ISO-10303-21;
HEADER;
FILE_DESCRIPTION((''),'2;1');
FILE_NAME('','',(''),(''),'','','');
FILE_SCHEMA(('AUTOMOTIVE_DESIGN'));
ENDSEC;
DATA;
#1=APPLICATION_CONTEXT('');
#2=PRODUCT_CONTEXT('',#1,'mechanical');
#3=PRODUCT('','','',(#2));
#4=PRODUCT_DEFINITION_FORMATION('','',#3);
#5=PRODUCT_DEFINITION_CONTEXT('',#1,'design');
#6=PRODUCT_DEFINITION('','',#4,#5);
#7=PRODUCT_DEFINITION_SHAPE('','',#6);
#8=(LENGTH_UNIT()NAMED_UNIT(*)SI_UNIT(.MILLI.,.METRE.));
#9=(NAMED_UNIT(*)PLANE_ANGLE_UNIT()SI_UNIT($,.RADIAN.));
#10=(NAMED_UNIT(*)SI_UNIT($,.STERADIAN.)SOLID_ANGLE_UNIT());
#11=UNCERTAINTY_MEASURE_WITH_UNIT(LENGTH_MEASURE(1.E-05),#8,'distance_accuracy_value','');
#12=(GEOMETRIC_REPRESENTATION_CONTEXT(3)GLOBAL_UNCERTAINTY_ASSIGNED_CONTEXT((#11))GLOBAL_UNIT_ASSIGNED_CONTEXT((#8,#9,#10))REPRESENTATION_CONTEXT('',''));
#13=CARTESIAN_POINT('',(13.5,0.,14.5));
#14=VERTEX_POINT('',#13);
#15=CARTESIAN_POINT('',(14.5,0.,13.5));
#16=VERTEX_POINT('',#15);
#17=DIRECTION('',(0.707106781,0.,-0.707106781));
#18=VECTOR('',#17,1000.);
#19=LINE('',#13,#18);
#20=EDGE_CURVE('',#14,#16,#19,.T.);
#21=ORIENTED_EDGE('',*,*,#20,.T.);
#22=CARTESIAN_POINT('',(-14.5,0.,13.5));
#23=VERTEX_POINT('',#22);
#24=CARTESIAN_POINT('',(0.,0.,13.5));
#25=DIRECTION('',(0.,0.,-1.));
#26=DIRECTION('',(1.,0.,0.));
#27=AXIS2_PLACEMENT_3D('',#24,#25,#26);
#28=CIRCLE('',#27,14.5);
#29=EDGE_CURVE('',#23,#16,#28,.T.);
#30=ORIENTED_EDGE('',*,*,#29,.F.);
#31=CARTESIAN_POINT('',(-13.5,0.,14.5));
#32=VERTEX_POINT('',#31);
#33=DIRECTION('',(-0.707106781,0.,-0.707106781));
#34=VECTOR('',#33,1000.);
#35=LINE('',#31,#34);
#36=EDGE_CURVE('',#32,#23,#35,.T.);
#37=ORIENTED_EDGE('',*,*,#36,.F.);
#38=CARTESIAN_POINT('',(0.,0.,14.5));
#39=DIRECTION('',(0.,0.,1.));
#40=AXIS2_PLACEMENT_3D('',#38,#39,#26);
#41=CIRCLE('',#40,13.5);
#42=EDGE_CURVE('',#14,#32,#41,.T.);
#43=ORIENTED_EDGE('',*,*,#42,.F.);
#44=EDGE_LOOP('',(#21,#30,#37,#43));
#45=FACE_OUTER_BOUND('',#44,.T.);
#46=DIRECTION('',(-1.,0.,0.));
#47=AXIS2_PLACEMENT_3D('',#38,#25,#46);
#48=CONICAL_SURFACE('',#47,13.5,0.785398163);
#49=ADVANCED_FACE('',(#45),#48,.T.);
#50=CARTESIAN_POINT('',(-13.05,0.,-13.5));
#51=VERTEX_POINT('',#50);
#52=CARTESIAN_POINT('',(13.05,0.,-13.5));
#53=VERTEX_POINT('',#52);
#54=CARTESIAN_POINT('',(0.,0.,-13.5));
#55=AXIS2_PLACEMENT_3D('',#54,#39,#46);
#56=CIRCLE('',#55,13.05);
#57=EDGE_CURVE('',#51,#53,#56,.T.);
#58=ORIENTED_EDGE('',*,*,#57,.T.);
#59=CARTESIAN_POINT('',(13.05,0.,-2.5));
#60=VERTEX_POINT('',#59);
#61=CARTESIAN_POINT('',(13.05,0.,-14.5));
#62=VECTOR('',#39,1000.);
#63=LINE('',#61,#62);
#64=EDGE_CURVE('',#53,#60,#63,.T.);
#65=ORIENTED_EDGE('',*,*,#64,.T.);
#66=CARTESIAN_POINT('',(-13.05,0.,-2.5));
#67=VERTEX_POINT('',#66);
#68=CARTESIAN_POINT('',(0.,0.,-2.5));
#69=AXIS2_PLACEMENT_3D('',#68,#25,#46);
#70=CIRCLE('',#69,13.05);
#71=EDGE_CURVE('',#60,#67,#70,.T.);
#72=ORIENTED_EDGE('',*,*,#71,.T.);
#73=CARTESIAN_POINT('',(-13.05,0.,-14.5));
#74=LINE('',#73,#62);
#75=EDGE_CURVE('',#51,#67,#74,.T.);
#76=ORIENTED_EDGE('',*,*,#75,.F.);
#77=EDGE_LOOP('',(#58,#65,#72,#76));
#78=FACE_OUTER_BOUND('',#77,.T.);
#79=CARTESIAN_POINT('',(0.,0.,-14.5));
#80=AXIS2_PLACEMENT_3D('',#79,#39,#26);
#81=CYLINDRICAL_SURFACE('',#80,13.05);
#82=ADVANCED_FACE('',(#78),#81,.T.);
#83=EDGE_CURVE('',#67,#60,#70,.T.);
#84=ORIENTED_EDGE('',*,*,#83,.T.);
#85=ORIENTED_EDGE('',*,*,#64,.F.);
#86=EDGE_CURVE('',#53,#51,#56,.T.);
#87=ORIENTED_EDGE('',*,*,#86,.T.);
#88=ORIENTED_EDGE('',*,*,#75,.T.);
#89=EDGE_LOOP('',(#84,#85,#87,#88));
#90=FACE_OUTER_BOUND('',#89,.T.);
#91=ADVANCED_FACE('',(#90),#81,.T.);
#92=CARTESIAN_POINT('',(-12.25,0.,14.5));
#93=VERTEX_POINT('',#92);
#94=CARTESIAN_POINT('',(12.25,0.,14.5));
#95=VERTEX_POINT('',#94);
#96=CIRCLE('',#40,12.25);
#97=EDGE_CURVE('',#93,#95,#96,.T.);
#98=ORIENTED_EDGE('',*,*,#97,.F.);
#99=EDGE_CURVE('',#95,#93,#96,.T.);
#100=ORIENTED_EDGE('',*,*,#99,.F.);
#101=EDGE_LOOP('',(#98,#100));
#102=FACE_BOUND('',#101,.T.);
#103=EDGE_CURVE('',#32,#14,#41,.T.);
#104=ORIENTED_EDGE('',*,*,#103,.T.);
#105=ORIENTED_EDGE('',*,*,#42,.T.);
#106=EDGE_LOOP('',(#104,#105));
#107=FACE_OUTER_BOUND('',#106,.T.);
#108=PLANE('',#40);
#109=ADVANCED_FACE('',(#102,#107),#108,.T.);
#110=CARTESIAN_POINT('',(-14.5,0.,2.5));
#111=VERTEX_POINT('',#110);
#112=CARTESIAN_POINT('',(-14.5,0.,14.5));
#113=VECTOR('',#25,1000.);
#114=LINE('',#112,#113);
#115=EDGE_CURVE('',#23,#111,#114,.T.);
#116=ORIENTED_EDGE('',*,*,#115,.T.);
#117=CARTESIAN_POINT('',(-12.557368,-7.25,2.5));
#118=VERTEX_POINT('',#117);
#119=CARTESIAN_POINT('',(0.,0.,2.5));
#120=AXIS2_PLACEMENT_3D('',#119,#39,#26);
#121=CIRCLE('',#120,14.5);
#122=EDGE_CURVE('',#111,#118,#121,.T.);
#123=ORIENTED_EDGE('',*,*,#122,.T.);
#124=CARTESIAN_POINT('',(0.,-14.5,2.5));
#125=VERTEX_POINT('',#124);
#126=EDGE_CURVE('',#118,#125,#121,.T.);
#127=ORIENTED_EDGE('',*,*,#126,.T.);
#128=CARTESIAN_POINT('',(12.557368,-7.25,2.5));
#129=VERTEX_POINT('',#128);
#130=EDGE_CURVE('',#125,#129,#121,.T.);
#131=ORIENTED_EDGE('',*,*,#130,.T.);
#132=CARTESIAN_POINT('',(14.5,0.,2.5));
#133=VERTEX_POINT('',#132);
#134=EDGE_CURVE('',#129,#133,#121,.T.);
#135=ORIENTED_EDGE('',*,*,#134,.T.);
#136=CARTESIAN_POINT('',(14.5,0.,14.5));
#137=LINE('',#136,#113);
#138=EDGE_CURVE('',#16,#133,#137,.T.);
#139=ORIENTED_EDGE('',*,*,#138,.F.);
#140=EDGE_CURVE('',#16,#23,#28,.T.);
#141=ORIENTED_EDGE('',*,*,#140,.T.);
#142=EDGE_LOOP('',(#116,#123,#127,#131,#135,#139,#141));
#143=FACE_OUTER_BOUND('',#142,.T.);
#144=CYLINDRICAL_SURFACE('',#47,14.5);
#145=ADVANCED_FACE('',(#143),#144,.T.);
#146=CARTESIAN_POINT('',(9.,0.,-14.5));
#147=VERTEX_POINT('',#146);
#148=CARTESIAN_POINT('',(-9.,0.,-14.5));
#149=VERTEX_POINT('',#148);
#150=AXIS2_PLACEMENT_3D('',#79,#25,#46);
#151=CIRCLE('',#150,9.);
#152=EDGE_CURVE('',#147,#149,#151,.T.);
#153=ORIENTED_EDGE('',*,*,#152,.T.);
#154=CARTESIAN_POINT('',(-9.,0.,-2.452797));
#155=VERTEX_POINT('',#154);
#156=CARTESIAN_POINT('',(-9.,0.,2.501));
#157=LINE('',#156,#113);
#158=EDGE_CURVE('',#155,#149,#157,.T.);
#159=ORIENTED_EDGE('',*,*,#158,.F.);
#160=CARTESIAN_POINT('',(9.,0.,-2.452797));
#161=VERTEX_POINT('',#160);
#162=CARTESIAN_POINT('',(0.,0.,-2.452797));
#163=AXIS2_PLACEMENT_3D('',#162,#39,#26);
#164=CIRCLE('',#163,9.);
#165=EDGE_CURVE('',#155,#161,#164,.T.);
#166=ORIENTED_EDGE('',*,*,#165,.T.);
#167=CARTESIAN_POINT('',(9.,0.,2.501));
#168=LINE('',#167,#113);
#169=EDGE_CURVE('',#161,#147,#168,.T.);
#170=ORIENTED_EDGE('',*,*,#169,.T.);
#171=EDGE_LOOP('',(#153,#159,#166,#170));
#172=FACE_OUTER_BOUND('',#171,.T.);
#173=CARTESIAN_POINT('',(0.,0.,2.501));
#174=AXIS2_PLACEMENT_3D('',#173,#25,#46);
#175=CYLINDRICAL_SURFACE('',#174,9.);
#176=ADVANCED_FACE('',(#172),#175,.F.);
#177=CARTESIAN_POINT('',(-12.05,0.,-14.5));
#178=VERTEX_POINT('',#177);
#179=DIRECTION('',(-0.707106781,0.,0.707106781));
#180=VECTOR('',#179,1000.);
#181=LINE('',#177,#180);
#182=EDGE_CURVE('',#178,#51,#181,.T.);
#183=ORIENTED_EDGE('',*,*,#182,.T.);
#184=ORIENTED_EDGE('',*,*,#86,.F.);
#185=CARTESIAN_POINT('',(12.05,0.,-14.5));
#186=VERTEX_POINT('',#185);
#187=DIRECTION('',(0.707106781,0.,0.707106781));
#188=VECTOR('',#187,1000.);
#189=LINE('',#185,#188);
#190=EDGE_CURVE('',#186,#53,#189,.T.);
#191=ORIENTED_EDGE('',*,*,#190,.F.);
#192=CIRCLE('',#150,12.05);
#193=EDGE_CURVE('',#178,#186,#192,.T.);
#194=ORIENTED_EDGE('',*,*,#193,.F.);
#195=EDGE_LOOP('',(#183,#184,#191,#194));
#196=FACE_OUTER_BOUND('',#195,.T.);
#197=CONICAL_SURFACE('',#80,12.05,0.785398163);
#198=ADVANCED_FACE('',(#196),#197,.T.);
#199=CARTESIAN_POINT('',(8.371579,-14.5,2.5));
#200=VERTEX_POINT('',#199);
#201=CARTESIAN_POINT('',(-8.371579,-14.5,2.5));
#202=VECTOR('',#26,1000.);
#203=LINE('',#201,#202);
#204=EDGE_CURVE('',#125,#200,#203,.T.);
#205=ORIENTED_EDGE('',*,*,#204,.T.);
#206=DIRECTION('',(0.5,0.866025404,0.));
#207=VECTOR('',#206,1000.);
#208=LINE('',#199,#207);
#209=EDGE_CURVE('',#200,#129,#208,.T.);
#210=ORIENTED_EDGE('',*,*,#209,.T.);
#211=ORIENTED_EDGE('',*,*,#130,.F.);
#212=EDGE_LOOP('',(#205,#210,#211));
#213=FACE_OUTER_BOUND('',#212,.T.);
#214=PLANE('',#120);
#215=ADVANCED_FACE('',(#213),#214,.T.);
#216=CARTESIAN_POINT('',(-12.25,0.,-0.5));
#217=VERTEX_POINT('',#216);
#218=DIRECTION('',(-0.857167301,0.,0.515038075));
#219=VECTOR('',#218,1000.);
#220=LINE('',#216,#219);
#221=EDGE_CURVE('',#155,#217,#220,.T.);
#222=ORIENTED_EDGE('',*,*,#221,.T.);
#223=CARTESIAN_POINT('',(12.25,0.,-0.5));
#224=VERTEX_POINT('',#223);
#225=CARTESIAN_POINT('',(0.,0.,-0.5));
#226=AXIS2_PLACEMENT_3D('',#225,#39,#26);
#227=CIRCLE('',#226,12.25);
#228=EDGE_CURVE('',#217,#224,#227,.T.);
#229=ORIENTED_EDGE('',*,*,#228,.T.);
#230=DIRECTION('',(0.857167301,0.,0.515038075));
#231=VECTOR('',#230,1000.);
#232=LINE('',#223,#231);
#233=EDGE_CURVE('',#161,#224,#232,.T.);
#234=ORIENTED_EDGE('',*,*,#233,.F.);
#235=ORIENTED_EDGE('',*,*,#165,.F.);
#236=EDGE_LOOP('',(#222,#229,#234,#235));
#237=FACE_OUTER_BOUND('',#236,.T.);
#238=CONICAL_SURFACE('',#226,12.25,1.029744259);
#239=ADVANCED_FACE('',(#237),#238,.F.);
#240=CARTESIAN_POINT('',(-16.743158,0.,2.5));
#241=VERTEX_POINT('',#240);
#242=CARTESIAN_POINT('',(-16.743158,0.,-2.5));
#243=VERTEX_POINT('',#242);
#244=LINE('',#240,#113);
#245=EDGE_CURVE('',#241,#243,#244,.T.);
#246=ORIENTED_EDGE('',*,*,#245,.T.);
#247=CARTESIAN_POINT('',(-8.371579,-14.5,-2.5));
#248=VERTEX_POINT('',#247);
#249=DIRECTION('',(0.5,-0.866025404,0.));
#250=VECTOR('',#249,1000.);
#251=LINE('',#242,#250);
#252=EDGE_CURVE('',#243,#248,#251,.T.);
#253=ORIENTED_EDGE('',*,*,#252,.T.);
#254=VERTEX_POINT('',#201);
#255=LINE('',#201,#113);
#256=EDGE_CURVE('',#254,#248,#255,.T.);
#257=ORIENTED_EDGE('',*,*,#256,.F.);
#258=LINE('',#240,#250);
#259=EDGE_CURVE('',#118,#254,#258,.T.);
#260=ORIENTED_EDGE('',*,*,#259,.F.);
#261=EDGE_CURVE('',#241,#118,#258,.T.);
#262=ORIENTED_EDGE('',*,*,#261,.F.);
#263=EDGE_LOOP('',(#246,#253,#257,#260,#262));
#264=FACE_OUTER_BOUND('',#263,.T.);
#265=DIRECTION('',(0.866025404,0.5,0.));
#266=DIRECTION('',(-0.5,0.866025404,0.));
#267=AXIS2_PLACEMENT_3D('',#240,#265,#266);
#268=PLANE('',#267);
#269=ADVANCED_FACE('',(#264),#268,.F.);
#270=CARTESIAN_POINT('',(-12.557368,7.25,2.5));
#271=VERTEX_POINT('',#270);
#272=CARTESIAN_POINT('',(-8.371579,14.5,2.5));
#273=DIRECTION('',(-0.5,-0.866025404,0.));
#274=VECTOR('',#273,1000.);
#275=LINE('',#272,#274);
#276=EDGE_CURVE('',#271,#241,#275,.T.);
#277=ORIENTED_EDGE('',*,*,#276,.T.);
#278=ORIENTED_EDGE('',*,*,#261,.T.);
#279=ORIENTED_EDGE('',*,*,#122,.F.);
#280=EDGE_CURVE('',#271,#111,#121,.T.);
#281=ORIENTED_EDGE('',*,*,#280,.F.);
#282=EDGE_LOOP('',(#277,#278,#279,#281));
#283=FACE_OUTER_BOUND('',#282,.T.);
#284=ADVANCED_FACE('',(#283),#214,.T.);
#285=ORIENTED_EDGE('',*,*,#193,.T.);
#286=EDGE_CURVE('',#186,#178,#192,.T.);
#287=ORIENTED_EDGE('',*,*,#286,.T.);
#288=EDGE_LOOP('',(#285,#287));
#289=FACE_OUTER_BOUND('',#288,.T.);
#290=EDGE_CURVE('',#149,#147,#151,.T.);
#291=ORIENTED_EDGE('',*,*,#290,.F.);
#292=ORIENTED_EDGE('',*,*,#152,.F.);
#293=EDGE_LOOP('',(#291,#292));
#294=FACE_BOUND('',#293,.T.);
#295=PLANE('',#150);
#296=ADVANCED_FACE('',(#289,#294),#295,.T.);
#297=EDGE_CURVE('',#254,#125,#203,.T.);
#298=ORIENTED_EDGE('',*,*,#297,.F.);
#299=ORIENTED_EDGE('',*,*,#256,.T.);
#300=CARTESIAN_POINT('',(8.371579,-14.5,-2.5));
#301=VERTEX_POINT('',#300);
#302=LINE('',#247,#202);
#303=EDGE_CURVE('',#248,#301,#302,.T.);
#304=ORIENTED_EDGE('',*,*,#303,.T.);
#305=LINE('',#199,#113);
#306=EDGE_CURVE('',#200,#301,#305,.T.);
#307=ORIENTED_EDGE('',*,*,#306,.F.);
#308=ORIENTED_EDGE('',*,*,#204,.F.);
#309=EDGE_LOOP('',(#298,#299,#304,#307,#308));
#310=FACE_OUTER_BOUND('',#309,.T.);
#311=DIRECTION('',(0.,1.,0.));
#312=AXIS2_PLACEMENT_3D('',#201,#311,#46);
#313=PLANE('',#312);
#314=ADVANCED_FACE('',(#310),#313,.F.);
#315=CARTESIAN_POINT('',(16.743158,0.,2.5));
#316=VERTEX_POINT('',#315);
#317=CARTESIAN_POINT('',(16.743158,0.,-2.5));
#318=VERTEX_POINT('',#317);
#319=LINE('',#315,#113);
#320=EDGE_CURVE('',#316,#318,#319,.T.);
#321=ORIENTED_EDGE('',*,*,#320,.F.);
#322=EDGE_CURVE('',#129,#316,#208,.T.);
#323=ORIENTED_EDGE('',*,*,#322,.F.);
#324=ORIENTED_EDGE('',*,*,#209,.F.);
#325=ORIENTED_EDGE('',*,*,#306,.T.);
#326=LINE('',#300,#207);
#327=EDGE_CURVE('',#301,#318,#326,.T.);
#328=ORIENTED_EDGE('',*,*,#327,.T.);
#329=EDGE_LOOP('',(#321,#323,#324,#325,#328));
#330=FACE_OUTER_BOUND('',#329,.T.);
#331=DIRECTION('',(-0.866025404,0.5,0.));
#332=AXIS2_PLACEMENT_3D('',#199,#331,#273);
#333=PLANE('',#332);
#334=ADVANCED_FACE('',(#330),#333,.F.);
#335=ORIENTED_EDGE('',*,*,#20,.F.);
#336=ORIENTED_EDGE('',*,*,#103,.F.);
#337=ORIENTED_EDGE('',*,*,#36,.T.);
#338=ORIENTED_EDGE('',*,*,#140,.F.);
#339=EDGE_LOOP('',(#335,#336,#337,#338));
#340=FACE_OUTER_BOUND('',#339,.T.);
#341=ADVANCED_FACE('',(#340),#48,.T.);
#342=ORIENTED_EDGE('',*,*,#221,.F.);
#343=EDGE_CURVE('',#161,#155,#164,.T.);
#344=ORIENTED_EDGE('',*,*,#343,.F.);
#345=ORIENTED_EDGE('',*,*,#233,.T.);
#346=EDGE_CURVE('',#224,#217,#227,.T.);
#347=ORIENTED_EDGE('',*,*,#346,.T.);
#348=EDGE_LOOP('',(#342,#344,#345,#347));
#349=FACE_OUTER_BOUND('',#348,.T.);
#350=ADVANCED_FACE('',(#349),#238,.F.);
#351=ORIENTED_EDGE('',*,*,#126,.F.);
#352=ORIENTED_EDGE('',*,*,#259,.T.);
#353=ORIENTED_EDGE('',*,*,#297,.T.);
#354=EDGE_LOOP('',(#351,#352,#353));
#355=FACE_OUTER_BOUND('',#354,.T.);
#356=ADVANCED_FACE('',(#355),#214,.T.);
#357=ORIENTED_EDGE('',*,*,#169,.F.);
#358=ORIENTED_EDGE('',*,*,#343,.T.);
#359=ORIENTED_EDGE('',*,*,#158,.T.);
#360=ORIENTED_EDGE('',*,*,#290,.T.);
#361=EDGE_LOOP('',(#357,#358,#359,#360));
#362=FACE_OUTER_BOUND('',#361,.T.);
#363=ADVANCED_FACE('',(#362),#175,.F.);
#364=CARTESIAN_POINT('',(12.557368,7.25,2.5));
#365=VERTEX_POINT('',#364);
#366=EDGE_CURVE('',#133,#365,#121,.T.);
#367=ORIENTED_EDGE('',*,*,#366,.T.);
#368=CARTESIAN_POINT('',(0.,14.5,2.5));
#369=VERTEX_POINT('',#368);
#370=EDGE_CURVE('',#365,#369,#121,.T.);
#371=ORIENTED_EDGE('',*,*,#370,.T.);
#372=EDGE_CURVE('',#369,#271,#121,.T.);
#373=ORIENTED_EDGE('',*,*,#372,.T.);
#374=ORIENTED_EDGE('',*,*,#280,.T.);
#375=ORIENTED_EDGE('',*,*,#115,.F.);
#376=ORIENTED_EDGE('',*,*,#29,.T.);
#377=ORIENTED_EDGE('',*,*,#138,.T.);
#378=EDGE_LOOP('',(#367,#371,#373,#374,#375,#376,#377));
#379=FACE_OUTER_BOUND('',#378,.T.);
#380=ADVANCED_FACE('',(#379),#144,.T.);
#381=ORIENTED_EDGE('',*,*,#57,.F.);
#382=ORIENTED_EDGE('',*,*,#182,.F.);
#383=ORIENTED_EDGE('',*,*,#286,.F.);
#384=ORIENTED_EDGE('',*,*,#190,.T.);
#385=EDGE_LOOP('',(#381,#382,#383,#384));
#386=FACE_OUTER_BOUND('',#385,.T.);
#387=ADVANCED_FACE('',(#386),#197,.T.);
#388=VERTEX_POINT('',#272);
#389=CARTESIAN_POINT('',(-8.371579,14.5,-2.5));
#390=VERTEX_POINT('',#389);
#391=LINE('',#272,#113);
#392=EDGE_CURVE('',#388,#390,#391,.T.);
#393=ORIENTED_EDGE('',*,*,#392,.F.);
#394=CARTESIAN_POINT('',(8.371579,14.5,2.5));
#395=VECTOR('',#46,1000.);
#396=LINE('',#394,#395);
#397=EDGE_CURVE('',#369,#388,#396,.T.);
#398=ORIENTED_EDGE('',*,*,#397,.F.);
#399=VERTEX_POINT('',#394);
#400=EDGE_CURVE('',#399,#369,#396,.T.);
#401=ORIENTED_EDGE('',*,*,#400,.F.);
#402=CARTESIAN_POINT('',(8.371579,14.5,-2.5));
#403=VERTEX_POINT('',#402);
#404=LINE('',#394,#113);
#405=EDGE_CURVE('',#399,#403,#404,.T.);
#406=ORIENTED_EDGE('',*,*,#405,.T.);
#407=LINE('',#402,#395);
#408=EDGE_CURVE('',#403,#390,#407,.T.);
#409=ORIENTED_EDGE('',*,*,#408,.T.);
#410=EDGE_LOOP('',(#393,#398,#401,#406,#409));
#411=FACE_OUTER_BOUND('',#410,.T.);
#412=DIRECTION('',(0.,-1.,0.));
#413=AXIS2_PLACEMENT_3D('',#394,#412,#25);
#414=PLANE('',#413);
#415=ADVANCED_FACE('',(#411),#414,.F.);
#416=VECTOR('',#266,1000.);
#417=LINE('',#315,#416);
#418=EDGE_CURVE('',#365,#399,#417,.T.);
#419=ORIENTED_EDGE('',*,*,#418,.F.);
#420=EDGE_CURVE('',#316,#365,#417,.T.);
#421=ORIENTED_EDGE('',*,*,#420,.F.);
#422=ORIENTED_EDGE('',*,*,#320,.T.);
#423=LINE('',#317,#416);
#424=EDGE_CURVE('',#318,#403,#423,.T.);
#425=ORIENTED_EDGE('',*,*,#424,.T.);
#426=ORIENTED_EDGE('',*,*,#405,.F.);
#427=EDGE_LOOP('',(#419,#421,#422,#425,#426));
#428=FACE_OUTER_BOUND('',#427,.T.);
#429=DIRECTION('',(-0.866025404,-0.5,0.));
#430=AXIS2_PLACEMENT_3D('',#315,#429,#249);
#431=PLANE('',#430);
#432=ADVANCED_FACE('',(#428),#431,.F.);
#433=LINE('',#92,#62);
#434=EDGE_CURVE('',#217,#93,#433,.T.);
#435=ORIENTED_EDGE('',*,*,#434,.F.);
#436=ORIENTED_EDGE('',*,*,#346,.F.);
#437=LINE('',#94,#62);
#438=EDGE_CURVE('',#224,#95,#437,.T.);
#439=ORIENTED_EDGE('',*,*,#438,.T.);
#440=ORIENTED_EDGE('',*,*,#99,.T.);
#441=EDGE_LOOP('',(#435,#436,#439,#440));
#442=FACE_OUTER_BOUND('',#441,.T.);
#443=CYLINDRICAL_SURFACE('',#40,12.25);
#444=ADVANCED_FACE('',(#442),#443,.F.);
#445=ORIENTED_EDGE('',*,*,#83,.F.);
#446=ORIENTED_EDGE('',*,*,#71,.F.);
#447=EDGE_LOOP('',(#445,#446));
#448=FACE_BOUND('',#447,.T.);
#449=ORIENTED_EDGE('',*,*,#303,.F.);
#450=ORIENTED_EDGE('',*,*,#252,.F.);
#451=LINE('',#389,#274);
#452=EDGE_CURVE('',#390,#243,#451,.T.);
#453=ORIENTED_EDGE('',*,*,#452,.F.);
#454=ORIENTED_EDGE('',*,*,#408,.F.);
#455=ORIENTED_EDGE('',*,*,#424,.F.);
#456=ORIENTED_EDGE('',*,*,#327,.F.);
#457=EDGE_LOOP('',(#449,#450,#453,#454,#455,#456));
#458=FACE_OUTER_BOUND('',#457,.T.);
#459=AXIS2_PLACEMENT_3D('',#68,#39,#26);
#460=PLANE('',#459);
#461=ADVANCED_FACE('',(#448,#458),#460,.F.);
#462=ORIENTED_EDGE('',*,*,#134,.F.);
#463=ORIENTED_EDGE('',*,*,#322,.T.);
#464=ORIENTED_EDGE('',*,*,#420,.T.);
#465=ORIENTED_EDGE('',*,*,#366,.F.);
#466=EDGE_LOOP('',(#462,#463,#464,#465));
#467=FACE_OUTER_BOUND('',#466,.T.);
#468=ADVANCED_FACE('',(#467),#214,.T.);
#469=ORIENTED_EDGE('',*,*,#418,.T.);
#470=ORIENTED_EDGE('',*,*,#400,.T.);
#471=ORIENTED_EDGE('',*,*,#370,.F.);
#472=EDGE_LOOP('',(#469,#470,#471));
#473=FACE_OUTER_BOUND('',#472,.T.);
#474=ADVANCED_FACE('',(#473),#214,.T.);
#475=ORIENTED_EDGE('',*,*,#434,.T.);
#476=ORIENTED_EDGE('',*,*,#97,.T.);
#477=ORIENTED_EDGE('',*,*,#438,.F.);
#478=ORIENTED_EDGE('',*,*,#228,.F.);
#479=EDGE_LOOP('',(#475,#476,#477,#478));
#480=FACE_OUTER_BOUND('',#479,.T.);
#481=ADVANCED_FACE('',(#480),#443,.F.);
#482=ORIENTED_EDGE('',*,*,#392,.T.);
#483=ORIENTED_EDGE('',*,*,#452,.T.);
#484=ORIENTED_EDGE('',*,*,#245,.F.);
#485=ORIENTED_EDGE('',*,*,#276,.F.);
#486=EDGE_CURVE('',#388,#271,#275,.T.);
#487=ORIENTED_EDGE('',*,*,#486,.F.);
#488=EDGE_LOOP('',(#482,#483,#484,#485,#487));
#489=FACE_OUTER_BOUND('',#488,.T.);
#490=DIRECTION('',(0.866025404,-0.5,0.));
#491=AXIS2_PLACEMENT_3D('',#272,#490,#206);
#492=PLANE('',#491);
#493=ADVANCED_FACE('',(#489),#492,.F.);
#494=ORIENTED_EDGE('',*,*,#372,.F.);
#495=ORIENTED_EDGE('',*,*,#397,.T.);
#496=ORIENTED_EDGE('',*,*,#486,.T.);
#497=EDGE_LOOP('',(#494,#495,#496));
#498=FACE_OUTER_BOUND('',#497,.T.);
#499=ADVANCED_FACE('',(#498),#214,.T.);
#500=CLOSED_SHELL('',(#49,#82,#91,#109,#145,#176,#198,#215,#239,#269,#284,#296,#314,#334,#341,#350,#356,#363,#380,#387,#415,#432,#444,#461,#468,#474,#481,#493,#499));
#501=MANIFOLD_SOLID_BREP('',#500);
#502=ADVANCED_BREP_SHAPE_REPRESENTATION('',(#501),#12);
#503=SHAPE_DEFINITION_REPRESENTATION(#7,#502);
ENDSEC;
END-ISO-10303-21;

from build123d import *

# Parameters (mm, degrees)
EXTRUDE_1_DEPTH          = 2.5
SKETCH_4_R               = 13.05
EXTRUDE_3_DEPTH          = 12
CUT_EXTRUDE_2_REACH      = 29.921
SKETCH_5_R               = 9
SKETCH_6_R               = 14.5
SKETCH_6_R_2             = 9
EXTRUDE_4_DEPTH          = 12
HOLE_WIZARD_G3_4_1_D     = 24.5
HOLE_WIZARD_G3_4_1_DEPTH = 15
HOLE_WIZARD_G3_4_1_TIP   = 7.360542583
CHAMFER_1_SIZE           = 1


with BuildPart() as part:
    # 草图1 → 凸台-拉伸1 (new, symmetric)
    with BuildSketch(Plane.XY):
        Polygon((16.743157806, 0), (8.371578903, 14.5), (-8.371578903, 14.5), (-16.743157806, 0), (-8.371578903, -14.5), (8.371578903, -14.5), align=None)
    extrude(amount=EXTRUDE_1_DEPTH, both=True)

    # 草图4 → 凸台-拉伸3 (add)
    with BuildSketch(Plane(origin=(0, 0, -2.5), x_dir=(-1, 0, 0), z_dir=(0, 0, -1))):
        Circle(SKETCH_4_R)
    extrude(amount=EXTRUDE_3_DEPTH)

    # 草图5 → 切除-拉伸2 (cut, up to next)
    with BuildSketch(Plane(origin=(0, 0, -14.5), x_dir=(-1, 0, 0), z_dir=(0, 0, -1)), mode=Mode.PRIVATE) as cut_extrude_2_sk1:
        Circle(SKETCH_5_R)
    cut_extrude_2_tool1 = extrude(cut_extrude_2_sk1.sketch, amount=-CUT_EXTRUDE_2_REACH, mode=Mode.PRIVATE) & part.part
    add(cut_extrude_2_tool1.solids().sort_by_distance((0, 0, -14.5))[0], mode=Mode.SUBTRACT)

    # 草图6 → 凸台-拉伸4 (add)
    with BuildSketch(Plane.XY.offset(2.5)):
        with Locations(Location((0, 0, 0), (0, 0, 150))):
            Circle(SKETCH_6_R)
        with Locations(Location((0, 0, 0), (0, 0, 180))):
            Circle(SKETCH_6_R_2, mode=Mode.SUBTRACT)
    extrude(amount=EXTRUDE_4_DEPTH)

    # G3/4 螺纹孔1
    with Locations(Plane.XY.offset(14.5)):
        with Locations((0, 0)):
            Hole(HOLE_WIZARD_G3_4_1_D / 2, depth=HOLE_WIZARD_G3_4_1_DEPTH)
            with Locations((0, 0, -(HOLE_WIZARD_G3_4_1_DEPTH + HOLE_WIZARD_G3_4_1_TIP / 2))):  # 118° drill point
                Cone(0, HOLE_WIZARD_G3_4_1_D / 2, HOLE_WIZARD_G3_4_1_TIP, mode=Mode.SUBTRACT)

    # 倒角1
    chamfer_1_edges = [part.edges().sort_by_distance(p)[0] for p in [
        (13.05, 0, -14.5),
        (12.557368355, -7.25, 14.5),
    ]]
    chamfer(chamfer_1_edges, length=CHAMFER_1_SIZE)


solid = part.part
